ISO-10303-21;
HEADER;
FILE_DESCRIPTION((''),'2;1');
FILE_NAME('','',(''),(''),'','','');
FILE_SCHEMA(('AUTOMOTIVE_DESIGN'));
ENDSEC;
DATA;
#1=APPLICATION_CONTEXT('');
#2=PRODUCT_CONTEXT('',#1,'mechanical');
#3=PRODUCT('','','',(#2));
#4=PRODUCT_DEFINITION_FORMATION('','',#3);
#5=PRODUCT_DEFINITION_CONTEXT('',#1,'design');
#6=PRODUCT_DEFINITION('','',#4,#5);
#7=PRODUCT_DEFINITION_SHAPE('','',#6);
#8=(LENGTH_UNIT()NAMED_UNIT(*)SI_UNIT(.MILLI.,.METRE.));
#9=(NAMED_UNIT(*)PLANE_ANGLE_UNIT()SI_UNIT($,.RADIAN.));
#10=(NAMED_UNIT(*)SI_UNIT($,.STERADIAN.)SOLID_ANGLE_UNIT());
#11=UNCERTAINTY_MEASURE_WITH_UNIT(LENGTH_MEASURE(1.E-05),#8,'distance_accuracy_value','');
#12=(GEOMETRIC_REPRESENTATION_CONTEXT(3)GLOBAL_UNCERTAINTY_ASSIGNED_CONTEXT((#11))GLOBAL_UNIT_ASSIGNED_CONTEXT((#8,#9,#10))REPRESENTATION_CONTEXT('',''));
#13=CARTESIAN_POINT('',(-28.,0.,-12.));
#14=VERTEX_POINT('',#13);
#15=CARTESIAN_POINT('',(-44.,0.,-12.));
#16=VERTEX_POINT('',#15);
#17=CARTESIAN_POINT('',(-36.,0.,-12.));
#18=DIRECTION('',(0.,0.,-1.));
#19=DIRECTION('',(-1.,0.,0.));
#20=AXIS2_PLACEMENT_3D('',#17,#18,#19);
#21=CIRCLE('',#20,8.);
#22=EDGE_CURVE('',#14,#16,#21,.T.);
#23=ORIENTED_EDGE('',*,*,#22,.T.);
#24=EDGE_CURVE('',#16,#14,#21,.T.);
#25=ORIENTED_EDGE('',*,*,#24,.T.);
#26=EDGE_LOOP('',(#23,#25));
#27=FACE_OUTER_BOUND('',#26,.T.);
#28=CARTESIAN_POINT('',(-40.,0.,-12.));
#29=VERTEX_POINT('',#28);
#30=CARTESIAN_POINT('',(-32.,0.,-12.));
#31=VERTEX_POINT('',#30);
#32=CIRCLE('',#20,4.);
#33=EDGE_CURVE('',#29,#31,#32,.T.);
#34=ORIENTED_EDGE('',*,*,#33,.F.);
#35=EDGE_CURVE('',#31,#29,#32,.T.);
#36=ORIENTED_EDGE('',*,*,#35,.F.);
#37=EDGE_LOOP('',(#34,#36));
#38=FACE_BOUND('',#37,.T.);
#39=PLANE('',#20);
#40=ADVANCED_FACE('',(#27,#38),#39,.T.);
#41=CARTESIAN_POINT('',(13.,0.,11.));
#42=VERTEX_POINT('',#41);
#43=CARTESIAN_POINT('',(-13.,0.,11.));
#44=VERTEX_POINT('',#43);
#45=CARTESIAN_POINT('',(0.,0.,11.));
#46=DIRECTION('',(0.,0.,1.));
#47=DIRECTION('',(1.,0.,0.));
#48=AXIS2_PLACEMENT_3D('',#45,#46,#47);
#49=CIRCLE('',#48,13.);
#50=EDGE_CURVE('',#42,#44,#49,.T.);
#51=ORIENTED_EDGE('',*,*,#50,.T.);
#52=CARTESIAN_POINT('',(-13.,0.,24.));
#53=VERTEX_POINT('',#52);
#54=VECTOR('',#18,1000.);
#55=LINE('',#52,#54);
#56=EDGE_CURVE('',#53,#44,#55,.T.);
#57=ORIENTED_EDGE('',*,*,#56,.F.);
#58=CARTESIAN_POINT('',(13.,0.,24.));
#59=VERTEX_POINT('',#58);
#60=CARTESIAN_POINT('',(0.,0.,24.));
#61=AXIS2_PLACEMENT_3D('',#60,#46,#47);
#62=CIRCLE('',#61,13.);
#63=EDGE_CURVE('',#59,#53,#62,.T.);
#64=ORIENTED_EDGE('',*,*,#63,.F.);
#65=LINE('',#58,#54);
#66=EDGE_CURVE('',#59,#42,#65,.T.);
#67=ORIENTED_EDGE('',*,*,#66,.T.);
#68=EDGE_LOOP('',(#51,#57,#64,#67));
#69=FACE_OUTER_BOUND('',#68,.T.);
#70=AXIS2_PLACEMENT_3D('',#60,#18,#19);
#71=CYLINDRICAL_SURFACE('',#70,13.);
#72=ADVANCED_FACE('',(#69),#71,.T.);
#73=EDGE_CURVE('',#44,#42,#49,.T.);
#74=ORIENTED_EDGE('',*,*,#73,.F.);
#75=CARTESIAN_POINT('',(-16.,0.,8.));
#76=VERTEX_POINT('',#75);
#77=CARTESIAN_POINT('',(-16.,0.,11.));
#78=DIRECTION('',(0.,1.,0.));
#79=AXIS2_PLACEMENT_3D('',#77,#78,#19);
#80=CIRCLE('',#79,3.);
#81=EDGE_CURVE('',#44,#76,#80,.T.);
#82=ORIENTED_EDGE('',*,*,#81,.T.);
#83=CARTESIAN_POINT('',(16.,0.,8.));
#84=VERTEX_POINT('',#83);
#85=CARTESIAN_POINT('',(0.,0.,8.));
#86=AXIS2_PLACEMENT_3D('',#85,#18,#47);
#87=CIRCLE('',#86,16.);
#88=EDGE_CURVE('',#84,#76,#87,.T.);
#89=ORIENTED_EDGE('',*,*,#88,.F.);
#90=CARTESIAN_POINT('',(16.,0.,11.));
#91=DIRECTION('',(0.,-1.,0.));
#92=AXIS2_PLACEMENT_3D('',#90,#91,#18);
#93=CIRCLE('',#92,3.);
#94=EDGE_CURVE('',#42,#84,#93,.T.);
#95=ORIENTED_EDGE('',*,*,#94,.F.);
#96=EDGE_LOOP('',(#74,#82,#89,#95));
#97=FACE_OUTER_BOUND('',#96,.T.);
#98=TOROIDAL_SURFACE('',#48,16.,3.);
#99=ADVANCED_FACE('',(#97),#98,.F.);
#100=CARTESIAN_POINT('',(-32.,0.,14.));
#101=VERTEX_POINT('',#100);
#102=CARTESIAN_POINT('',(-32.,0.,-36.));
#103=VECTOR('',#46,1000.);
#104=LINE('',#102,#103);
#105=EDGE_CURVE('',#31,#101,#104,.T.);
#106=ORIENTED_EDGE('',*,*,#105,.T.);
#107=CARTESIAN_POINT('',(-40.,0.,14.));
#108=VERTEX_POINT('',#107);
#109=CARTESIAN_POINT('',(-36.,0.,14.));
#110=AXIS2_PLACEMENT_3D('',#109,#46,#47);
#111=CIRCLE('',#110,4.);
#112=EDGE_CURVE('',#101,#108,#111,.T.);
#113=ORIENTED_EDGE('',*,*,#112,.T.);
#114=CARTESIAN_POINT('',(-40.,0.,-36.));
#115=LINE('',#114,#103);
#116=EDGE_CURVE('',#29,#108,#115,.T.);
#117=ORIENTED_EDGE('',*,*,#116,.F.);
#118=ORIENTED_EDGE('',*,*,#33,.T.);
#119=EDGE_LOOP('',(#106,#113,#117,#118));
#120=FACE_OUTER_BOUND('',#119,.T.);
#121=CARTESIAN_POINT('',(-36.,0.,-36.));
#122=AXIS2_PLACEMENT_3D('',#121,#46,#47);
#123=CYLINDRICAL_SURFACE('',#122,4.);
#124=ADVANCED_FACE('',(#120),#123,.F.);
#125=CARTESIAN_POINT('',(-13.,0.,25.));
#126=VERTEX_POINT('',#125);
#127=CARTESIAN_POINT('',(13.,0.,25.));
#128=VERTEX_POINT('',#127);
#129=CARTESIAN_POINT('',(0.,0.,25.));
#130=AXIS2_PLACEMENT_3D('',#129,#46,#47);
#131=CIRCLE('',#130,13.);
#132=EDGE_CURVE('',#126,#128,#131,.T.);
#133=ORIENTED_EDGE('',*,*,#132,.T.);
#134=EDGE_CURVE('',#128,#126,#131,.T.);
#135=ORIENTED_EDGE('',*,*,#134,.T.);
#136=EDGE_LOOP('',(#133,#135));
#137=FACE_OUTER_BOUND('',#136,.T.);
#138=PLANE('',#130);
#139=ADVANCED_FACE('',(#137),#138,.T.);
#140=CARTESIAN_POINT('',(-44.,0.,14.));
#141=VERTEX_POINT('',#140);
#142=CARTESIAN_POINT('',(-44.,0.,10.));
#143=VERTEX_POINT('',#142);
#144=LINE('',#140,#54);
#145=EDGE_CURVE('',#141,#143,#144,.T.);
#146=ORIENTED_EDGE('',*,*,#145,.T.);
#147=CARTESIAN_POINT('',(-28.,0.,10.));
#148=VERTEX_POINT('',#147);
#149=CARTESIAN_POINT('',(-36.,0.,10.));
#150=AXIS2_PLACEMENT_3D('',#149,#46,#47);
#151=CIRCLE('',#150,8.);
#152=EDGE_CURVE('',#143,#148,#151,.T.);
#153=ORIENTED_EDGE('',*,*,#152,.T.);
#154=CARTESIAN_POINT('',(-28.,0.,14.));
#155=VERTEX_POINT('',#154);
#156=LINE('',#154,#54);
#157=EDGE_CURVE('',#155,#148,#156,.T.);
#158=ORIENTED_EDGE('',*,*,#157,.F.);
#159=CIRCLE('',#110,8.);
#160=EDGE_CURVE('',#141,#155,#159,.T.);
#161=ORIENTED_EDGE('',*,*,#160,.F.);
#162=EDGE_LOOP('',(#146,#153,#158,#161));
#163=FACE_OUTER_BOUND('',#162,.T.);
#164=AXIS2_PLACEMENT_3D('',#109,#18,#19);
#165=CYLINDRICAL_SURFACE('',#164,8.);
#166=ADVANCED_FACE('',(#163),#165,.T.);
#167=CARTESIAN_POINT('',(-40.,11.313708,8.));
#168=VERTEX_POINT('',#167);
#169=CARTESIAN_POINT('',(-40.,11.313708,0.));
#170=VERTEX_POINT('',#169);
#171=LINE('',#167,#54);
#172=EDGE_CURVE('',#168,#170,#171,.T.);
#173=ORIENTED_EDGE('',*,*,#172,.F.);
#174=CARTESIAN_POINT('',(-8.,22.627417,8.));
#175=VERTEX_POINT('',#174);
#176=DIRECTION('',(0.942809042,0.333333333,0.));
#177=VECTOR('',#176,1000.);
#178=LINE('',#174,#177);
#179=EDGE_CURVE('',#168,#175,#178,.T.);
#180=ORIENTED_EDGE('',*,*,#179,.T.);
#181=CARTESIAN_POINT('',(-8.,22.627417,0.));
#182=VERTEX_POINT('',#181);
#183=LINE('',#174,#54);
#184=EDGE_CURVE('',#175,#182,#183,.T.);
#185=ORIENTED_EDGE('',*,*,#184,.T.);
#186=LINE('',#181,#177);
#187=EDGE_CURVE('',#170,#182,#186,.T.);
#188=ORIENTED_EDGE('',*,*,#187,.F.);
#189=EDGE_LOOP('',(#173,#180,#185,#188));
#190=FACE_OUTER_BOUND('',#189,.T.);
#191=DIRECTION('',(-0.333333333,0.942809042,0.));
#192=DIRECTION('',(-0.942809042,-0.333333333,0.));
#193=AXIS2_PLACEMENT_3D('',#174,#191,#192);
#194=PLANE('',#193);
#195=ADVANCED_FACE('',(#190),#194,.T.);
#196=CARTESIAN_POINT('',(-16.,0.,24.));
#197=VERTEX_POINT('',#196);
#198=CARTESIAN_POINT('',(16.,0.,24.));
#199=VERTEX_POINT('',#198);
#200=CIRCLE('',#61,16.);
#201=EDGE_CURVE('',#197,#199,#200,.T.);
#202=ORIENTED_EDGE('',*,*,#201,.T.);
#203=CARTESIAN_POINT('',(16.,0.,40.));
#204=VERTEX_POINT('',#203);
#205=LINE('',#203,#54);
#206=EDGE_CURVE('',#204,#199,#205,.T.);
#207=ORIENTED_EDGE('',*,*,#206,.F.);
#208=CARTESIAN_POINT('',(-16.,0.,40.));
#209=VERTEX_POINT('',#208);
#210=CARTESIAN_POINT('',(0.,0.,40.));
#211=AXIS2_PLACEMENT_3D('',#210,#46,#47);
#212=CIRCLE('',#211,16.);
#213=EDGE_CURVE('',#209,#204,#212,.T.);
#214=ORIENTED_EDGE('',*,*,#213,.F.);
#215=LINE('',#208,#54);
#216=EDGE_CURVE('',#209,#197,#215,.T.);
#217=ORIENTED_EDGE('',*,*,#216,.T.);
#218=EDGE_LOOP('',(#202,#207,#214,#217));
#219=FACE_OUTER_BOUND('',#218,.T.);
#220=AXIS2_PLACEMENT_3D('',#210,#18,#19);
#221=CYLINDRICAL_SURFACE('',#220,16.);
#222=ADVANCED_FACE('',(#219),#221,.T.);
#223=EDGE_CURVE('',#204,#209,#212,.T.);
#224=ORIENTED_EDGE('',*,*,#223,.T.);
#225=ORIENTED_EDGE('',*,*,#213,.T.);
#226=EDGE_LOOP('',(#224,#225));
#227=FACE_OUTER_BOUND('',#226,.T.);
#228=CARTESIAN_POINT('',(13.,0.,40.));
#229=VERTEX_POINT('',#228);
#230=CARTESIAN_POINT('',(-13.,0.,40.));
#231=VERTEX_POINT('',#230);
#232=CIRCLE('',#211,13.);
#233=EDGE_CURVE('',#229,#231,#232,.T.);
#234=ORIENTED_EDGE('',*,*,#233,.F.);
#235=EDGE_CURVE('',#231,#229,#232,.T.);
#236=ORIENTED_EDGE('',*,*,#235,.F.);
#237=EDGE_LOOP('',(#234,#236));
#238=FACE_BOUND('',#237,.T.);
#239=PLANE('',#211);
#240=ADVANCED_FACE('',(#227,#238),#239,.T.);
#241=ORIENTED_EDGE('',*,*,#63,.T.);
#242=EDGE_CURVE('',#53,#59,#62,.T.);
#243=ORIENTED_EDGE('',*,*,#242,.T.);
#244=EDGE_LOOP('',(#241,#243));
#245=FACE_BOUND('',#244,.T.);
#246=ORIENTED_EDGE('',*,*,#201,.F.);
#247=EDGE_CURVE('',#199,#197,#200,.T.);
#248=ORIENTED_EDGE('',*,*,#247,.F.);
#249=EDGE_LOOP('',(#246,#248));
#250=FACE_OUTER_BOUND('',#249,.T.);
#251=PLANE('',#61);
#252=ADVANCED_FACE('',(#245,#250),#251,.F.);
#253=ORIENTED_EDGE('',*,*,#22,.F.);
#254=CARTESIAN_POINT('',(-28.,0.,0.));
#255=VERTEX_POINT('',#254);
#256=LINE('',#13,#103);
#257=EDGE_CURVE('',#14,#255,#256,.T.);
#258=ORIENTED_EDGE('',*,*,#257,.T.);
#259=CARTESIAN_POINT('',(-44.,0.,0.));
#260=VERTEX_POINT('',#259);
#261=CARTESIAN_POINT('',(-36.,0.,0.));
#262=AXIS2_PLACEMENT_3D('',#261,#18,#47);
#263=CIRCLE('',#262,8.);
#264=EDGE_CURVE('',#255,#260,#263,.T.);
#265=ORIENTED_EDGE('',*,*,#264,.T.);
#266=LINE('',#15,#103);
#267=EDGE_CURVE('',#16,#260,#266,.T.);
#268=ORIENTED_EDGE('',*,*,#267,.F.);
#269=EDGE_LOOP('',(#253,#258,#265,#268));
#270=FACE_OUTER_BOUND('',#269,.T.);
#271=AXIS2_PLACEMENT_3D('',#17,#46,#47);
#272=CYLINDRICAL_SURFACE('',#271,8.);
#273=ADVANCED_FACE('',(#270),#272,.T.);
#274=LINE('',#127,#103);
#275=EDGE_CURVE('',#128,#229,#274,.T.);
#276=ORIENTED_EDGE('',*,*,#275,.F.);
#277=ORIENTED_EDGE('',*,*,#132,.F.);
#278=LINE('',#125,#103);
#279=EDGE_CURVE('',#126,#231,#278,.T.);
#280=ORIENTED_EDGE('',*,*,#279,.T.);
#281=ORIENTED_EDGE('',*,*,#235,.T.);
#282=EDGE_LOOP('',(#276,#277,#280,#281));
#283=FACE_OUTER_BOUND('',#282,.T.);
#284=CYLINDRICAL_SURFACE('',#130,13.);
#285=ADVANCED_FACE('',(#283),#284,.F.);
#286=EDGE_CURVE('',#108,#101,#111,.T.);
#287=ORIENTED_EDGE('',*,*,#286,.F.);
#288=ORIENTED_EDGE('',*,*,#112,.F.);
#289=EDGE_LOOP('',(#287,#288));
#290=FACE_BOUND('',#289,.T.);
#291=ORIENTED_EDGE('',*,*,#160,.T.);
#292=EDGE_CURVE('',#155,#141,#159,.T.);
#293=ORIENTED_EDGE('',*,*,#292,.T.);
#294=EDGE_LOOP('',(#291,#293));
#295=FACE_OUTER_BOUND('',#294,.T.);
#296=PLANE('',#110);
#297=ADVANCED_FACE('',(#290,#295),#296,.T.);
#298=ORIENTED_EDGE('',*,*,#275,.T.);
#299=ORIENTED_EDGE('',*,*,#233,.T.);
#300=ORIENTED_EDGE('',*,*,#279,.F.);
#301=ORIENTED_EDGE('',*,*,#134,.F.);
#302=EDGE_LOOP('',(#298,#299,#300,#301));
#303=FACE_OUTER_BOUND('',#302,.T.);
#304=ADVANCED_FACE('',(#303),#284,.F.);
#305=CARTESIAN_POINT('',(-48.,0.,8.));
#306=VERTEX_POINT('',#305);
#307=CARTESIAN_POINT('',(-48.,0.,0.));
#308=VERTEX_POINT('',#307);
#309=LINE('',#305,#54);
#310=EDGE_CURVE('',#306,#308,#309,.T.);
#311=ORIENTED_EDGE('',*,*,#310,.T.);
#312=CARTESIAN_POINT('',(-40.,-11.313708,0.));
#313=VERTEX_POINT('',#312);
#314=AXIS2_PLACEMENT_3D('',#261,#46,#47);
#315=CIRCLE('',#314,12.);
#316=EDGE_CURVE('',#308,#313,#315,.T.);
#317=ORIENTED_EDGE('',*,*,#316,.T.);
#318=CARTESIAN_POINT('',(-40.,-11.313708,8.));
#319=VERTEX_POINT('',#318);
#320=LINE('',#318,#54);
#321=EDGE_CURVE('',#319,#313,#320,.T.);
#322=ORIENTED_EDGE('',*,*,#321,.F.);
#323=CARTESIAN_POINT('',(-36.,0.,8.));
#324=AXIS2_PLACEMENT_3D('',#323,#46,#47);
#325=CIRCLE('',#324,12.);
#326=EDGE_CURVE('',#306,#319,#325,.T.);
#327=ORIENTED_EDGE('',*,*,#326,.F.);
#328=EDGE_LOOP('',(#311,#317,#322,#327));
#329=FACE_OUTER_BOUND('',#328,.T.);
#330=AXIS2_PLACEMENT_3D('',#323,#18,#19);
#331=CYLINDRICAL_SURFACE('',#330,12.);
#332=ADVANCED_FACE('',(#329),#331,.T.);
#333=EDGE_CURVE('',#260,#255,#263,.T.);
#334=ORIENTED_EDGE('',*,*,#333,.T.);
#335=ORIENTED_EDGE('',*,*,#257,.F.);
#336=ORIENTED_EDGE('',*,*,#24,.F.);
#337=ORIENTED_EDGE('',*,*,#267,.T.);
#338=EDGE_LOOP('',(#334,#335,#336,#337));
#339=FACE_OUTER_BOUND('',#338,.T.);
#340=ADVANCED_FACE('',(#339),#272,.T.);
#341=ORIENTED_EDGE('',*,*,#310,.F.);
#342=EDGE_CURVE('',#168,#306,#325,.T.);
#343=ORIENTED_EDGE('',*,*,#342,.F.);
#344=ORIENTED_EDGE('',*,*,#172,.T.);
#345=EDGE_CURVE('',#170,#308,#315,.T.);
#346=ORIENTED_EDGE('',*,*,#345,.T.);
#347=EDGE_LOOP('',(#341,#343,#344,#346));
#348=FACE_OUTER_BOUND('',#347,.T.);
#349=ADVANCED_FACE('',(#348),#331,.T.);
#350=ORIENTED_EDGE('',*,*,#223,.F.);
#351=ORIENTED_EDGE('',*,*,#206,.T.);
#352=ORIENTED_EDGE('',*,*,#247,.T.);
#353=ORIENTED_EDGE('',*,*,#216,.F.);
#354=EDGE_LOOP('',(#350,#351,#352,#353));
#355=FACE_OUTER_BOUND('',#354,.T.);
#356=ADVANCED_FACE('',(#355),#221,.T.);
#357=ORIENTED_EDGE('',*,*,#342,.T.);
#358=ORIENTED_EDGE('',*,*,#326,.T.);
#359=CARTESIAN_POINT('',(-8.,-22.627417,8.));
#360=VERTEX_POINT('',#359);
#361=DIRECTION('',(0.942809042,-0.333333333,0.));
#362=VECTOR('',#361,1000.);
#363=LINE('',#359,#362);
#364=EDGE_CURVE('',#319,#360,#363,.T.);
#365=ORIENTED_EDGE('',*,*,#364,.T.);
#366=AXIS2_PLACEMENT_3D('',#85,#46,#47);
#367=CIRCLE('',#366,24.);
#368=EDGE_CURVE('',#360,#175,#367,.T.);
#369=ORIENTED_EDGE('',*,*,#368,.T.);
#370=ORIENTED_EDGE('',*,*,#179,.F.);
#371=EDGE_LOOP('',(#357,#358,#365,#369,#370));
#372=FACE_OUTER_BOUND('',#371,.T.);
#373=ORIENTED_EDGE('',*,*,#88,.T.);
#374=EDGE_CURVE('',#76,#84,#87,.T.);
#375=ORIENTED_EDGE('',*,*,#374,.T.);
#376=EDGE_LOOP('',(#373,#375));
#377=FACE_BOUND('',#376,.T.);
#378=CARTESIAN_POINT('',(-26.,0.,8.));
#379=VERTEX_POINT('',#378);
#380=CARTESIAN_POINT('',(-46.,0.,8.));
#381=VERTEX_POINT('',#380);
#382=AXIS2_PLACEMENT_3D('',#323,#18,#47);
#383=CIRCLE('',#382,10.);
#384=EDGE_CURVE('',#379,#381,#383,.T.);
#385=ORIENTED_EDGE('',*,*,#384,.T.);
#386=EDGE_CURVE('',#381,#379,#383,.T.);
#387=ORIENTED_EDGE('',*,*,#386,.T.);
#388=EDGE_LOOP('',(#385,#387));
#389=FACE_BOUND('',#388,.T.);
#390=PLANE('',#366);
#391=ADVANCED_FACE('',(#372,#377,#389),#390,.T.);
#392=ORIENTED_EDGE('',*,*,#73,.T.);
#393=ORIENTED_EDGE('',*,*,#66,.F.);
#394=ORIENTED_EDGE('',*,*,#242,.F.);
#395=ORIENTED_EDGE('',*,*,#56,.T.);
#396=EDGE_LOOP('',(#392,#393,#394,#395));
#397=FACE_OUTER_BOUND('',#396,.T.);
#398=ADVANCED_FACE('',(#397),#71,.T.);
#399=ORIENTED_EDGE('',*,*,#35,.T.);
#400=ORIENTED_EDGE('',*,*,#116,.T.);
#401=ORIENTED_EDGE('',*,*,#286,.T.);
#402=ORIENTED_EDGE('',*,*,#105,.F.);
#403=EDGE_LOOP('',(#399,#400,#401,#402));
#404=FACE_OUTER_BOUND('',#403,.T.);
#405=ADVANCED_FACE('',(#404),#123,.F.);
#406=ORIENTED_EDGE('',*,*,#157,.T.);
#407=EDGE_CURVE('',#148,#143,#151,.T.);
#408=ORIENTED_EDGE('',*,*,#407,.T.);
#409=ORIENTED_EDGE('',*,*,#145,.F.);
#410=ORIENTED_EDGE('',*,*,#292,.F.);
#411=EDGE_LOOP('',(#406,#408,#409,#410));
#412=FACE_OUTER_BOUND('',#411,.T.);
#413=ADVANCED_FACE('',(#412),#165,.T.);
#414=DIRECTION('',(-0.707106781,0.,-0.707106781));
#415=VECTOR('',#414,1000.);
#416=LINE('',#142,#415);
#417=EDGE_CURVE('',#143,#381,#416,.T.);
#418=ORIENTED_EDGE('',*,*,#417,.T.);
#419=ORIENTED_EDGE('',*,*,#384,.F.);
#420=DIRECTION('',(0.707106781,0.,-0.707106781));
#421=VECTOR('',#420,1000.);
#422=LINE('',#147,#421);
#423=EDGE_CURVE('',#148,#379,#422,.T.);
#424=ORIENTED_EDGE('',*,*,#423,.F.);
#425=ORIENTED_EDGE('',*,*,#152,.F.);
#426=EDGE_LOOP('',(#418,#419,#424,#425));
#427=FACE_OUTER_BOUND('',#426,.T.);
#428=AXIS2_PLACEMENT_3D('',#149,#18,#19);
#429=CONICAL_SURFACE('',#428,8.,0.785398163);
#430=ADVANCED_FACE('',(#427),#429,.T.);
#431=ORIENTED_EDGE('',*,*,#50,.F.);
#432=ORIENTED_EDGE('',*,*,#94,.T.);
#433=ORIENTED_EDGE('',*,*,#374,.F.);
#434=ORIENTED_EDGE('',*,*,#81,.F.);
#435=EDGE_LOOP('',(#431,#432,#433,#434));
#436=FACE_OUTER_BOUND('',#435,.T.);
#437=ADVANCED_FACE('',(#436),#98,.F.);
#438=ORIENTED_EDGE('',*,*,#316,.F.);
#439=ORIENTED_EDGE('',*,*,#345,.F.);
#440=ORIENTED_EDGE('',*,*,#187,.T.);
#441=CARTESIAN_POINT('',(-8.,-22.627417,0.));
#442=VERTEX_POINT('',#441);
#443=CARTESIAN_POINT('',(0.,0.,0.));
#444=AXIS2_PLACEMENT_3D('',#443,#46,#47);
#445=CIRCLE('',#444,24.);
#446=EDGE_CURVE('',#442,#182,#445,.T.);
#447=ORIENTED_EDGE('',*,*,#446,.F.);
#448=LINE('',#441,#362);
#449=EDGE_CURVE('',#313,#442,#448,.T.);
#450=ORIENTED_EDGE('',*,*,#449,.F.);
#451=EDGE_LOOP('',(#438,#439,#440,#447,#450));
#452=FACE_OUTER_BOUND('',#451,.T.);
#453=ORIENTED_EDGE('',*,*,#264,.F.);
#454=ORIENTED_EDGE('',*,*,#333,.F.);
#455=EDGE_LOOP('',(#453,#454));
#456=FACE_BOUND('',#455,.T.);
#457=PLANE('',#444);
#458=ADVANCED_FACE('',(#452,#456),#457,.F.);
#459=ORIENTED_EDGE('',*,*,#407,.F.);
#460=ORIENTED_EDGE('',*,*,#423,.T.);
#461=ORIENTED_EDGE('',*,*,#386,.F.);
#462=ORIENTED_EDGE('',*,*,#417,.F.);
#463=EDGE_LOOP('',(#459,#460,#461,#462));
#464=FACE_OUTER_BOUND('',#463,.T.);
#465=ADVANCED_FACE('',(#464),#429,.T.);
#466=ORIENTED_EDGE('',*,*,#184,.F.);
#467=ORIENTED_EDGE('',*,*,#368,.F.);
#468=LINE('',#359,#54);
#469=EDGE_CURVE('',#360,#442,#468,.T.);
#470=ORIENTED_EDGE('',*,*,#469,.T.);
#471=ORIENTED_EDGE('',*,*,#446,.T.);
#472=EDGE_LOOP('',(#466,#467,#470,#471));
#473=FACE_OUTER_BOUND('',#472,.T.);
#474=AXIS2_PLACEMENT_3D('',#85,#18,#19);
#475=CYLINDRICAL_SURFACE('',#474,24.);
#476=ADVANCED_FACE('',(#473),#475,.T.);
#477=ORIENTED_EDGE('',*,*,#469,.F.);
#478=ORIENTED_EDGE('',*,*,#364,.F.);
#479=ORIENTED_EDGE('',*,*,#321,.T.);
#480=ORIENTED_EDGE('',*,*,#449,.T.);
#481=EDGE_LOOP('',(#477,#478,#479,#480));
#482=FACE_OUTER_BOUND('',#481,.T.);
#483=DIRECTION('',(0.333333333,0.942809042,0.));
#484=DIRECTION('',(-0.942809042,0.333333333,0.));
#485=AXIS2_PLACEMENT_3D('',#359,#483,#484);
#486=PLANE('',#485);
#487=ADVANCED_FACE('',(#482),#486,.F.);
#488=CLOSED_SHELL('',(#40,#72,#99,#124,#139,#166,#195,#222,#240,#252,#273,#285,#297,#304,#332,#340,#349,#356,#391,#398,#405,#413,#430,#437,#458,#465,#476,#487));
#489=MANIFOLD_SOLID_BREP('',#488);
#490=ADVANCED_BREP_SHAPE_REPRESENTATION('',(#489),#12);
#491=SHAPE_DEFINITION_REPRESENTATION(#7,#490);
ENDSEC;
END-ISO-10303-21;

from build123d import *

# Parameters (mm, degrees)
OVAL_PLATE_DEPTH           = 8
PIN_BOSS_SKETCH_R          = 8
PIN_BOSS_DEPTH             = 6
REAR_START                 = 12
REAR_BOSS_SKETCH_R         = 8
REAR_BOSS_DEPTH            = 12
TUBE_NECK_SKETCH_R         = 13
TUBE_NECK_26_DEPTH         = 16
TUBE_BOSS_SKETCH_R         = 16
TUBE_BOSS_32_DEPTH         = 16
TUBE_START                 = -15
TUBE_BORE_SKETCH_R         = 13
TUBE_BORE_26_DEPTH         = 15
TUBE_NECK_ROOT_FILLET_R3_R = 3
PIN_BOSS_CHAMFER_2MM_SIZE  = 2
PIN_HOLE_SKETCH_R          = 4
PIN_THROUGH_HOLE_DEPTH     = 50


with BuildPart() as part:
    # Oval Plate Sketch → Oval Plate (new body)
    with BuildSketch(Plane.XY):
        with BuildLine():
            Line((-40, 11.313708499), (-8, 22.627416998))
            ThreePointArc((-8, 22.627416998), (24, 0), (-8, -22.627416998))
            Line((-8, -22.627416998), (-40, -11.313708499))
            ThreePointArc((-40, -11.313708499), (-48, 0), (-40, 11.313708499))
        make_face()
    extrude(amount=OVAL_PLATE_DEPTH)

    # Pin Boss Sketch → Pin Boss (add)
    with BuildSketch(Plane.XY.offset(8)):
        with Locations((-36, 0)):
            Circle(PIN_BOSS_SKETCH_R)
    extrude(amount=PIN_BOSS_DEPTH)

    # Rear Boss Sketch → Rear Boss (add)
    with BuildSketch(Plane(origin=(0, 0, 0), x_dir=(-1, 0, 0), z_dir=(0, 0, -1)).offset(REAR_START)):
        with Locations(Location((36, 0, 0), (0, 0, 180))):
            Circle(REAR_BOSS_SKETCH_R)
    extrude(amount=-REAR_BOSS_DEPTH)

    # Tube Neck Sketch → Tube Neck Ø26 (add)
    with BuildSketch(Plane.XY.offset(8)):
        Circle(TUBE_NECK_SKETCH_R)
    extrude(amount=TUBE_NECK_26_DEPTH)

    # Tube Boss Sketch → Tube Boss Ø32 (add)
    with BuildSketch(Plane.XY.offset(24)):
        Circle(TUBE_BOSS_SKETCH_R)
    extrude(amount=TUBE_BOSS_32_DEPTH)

    # Tube Bore Sketch → Tube Bore Ø26 (cut)
    with BuildSketch(Plane.XY.offset(40).offset(TUBE_START)):
        Circle(TUBE_BORE_SKETCH_R)
    extrude(amount=TUBE_BORE_26_DEPTH, mode=Mode.SUBTRACT)

    # Tube Neck Root Fillet R3
    tube_neck_root_fillet_r3_edges = [part.edges().sort_by_distance(p)[0] for p in [
        (-13, 0, 8),
    ]]
    fillet(tube_neck_root_fillet_r3_edges, radius=TUBE_NECK_ROOT_FILLET_R3_R)

    # Pin Boss Chamfer 2mm
    pin_boss_chamfer_2mm_edges = [part.edges().sort_by_distance(p)[0] for p in [
        (-44, 0, 8),
    ]]
    chamfer(pin_boss_chamfer_2mm_edges, length=PIN_BOSS_CHAMFER_2MM_SIZE)

    # Pin Hole Sketch → Pin Through Hole (cut)
    with BuildSketch(Plane.XY.offset(14)):
        with Locations((-36, 0)):
            Circle(PIN_HOLE_SKETCH_R)
    extrude(amount=-PIN_THROUGH_HOLE_DEPTH, mode=Mode.SUBTRACT)


solid = part.part
